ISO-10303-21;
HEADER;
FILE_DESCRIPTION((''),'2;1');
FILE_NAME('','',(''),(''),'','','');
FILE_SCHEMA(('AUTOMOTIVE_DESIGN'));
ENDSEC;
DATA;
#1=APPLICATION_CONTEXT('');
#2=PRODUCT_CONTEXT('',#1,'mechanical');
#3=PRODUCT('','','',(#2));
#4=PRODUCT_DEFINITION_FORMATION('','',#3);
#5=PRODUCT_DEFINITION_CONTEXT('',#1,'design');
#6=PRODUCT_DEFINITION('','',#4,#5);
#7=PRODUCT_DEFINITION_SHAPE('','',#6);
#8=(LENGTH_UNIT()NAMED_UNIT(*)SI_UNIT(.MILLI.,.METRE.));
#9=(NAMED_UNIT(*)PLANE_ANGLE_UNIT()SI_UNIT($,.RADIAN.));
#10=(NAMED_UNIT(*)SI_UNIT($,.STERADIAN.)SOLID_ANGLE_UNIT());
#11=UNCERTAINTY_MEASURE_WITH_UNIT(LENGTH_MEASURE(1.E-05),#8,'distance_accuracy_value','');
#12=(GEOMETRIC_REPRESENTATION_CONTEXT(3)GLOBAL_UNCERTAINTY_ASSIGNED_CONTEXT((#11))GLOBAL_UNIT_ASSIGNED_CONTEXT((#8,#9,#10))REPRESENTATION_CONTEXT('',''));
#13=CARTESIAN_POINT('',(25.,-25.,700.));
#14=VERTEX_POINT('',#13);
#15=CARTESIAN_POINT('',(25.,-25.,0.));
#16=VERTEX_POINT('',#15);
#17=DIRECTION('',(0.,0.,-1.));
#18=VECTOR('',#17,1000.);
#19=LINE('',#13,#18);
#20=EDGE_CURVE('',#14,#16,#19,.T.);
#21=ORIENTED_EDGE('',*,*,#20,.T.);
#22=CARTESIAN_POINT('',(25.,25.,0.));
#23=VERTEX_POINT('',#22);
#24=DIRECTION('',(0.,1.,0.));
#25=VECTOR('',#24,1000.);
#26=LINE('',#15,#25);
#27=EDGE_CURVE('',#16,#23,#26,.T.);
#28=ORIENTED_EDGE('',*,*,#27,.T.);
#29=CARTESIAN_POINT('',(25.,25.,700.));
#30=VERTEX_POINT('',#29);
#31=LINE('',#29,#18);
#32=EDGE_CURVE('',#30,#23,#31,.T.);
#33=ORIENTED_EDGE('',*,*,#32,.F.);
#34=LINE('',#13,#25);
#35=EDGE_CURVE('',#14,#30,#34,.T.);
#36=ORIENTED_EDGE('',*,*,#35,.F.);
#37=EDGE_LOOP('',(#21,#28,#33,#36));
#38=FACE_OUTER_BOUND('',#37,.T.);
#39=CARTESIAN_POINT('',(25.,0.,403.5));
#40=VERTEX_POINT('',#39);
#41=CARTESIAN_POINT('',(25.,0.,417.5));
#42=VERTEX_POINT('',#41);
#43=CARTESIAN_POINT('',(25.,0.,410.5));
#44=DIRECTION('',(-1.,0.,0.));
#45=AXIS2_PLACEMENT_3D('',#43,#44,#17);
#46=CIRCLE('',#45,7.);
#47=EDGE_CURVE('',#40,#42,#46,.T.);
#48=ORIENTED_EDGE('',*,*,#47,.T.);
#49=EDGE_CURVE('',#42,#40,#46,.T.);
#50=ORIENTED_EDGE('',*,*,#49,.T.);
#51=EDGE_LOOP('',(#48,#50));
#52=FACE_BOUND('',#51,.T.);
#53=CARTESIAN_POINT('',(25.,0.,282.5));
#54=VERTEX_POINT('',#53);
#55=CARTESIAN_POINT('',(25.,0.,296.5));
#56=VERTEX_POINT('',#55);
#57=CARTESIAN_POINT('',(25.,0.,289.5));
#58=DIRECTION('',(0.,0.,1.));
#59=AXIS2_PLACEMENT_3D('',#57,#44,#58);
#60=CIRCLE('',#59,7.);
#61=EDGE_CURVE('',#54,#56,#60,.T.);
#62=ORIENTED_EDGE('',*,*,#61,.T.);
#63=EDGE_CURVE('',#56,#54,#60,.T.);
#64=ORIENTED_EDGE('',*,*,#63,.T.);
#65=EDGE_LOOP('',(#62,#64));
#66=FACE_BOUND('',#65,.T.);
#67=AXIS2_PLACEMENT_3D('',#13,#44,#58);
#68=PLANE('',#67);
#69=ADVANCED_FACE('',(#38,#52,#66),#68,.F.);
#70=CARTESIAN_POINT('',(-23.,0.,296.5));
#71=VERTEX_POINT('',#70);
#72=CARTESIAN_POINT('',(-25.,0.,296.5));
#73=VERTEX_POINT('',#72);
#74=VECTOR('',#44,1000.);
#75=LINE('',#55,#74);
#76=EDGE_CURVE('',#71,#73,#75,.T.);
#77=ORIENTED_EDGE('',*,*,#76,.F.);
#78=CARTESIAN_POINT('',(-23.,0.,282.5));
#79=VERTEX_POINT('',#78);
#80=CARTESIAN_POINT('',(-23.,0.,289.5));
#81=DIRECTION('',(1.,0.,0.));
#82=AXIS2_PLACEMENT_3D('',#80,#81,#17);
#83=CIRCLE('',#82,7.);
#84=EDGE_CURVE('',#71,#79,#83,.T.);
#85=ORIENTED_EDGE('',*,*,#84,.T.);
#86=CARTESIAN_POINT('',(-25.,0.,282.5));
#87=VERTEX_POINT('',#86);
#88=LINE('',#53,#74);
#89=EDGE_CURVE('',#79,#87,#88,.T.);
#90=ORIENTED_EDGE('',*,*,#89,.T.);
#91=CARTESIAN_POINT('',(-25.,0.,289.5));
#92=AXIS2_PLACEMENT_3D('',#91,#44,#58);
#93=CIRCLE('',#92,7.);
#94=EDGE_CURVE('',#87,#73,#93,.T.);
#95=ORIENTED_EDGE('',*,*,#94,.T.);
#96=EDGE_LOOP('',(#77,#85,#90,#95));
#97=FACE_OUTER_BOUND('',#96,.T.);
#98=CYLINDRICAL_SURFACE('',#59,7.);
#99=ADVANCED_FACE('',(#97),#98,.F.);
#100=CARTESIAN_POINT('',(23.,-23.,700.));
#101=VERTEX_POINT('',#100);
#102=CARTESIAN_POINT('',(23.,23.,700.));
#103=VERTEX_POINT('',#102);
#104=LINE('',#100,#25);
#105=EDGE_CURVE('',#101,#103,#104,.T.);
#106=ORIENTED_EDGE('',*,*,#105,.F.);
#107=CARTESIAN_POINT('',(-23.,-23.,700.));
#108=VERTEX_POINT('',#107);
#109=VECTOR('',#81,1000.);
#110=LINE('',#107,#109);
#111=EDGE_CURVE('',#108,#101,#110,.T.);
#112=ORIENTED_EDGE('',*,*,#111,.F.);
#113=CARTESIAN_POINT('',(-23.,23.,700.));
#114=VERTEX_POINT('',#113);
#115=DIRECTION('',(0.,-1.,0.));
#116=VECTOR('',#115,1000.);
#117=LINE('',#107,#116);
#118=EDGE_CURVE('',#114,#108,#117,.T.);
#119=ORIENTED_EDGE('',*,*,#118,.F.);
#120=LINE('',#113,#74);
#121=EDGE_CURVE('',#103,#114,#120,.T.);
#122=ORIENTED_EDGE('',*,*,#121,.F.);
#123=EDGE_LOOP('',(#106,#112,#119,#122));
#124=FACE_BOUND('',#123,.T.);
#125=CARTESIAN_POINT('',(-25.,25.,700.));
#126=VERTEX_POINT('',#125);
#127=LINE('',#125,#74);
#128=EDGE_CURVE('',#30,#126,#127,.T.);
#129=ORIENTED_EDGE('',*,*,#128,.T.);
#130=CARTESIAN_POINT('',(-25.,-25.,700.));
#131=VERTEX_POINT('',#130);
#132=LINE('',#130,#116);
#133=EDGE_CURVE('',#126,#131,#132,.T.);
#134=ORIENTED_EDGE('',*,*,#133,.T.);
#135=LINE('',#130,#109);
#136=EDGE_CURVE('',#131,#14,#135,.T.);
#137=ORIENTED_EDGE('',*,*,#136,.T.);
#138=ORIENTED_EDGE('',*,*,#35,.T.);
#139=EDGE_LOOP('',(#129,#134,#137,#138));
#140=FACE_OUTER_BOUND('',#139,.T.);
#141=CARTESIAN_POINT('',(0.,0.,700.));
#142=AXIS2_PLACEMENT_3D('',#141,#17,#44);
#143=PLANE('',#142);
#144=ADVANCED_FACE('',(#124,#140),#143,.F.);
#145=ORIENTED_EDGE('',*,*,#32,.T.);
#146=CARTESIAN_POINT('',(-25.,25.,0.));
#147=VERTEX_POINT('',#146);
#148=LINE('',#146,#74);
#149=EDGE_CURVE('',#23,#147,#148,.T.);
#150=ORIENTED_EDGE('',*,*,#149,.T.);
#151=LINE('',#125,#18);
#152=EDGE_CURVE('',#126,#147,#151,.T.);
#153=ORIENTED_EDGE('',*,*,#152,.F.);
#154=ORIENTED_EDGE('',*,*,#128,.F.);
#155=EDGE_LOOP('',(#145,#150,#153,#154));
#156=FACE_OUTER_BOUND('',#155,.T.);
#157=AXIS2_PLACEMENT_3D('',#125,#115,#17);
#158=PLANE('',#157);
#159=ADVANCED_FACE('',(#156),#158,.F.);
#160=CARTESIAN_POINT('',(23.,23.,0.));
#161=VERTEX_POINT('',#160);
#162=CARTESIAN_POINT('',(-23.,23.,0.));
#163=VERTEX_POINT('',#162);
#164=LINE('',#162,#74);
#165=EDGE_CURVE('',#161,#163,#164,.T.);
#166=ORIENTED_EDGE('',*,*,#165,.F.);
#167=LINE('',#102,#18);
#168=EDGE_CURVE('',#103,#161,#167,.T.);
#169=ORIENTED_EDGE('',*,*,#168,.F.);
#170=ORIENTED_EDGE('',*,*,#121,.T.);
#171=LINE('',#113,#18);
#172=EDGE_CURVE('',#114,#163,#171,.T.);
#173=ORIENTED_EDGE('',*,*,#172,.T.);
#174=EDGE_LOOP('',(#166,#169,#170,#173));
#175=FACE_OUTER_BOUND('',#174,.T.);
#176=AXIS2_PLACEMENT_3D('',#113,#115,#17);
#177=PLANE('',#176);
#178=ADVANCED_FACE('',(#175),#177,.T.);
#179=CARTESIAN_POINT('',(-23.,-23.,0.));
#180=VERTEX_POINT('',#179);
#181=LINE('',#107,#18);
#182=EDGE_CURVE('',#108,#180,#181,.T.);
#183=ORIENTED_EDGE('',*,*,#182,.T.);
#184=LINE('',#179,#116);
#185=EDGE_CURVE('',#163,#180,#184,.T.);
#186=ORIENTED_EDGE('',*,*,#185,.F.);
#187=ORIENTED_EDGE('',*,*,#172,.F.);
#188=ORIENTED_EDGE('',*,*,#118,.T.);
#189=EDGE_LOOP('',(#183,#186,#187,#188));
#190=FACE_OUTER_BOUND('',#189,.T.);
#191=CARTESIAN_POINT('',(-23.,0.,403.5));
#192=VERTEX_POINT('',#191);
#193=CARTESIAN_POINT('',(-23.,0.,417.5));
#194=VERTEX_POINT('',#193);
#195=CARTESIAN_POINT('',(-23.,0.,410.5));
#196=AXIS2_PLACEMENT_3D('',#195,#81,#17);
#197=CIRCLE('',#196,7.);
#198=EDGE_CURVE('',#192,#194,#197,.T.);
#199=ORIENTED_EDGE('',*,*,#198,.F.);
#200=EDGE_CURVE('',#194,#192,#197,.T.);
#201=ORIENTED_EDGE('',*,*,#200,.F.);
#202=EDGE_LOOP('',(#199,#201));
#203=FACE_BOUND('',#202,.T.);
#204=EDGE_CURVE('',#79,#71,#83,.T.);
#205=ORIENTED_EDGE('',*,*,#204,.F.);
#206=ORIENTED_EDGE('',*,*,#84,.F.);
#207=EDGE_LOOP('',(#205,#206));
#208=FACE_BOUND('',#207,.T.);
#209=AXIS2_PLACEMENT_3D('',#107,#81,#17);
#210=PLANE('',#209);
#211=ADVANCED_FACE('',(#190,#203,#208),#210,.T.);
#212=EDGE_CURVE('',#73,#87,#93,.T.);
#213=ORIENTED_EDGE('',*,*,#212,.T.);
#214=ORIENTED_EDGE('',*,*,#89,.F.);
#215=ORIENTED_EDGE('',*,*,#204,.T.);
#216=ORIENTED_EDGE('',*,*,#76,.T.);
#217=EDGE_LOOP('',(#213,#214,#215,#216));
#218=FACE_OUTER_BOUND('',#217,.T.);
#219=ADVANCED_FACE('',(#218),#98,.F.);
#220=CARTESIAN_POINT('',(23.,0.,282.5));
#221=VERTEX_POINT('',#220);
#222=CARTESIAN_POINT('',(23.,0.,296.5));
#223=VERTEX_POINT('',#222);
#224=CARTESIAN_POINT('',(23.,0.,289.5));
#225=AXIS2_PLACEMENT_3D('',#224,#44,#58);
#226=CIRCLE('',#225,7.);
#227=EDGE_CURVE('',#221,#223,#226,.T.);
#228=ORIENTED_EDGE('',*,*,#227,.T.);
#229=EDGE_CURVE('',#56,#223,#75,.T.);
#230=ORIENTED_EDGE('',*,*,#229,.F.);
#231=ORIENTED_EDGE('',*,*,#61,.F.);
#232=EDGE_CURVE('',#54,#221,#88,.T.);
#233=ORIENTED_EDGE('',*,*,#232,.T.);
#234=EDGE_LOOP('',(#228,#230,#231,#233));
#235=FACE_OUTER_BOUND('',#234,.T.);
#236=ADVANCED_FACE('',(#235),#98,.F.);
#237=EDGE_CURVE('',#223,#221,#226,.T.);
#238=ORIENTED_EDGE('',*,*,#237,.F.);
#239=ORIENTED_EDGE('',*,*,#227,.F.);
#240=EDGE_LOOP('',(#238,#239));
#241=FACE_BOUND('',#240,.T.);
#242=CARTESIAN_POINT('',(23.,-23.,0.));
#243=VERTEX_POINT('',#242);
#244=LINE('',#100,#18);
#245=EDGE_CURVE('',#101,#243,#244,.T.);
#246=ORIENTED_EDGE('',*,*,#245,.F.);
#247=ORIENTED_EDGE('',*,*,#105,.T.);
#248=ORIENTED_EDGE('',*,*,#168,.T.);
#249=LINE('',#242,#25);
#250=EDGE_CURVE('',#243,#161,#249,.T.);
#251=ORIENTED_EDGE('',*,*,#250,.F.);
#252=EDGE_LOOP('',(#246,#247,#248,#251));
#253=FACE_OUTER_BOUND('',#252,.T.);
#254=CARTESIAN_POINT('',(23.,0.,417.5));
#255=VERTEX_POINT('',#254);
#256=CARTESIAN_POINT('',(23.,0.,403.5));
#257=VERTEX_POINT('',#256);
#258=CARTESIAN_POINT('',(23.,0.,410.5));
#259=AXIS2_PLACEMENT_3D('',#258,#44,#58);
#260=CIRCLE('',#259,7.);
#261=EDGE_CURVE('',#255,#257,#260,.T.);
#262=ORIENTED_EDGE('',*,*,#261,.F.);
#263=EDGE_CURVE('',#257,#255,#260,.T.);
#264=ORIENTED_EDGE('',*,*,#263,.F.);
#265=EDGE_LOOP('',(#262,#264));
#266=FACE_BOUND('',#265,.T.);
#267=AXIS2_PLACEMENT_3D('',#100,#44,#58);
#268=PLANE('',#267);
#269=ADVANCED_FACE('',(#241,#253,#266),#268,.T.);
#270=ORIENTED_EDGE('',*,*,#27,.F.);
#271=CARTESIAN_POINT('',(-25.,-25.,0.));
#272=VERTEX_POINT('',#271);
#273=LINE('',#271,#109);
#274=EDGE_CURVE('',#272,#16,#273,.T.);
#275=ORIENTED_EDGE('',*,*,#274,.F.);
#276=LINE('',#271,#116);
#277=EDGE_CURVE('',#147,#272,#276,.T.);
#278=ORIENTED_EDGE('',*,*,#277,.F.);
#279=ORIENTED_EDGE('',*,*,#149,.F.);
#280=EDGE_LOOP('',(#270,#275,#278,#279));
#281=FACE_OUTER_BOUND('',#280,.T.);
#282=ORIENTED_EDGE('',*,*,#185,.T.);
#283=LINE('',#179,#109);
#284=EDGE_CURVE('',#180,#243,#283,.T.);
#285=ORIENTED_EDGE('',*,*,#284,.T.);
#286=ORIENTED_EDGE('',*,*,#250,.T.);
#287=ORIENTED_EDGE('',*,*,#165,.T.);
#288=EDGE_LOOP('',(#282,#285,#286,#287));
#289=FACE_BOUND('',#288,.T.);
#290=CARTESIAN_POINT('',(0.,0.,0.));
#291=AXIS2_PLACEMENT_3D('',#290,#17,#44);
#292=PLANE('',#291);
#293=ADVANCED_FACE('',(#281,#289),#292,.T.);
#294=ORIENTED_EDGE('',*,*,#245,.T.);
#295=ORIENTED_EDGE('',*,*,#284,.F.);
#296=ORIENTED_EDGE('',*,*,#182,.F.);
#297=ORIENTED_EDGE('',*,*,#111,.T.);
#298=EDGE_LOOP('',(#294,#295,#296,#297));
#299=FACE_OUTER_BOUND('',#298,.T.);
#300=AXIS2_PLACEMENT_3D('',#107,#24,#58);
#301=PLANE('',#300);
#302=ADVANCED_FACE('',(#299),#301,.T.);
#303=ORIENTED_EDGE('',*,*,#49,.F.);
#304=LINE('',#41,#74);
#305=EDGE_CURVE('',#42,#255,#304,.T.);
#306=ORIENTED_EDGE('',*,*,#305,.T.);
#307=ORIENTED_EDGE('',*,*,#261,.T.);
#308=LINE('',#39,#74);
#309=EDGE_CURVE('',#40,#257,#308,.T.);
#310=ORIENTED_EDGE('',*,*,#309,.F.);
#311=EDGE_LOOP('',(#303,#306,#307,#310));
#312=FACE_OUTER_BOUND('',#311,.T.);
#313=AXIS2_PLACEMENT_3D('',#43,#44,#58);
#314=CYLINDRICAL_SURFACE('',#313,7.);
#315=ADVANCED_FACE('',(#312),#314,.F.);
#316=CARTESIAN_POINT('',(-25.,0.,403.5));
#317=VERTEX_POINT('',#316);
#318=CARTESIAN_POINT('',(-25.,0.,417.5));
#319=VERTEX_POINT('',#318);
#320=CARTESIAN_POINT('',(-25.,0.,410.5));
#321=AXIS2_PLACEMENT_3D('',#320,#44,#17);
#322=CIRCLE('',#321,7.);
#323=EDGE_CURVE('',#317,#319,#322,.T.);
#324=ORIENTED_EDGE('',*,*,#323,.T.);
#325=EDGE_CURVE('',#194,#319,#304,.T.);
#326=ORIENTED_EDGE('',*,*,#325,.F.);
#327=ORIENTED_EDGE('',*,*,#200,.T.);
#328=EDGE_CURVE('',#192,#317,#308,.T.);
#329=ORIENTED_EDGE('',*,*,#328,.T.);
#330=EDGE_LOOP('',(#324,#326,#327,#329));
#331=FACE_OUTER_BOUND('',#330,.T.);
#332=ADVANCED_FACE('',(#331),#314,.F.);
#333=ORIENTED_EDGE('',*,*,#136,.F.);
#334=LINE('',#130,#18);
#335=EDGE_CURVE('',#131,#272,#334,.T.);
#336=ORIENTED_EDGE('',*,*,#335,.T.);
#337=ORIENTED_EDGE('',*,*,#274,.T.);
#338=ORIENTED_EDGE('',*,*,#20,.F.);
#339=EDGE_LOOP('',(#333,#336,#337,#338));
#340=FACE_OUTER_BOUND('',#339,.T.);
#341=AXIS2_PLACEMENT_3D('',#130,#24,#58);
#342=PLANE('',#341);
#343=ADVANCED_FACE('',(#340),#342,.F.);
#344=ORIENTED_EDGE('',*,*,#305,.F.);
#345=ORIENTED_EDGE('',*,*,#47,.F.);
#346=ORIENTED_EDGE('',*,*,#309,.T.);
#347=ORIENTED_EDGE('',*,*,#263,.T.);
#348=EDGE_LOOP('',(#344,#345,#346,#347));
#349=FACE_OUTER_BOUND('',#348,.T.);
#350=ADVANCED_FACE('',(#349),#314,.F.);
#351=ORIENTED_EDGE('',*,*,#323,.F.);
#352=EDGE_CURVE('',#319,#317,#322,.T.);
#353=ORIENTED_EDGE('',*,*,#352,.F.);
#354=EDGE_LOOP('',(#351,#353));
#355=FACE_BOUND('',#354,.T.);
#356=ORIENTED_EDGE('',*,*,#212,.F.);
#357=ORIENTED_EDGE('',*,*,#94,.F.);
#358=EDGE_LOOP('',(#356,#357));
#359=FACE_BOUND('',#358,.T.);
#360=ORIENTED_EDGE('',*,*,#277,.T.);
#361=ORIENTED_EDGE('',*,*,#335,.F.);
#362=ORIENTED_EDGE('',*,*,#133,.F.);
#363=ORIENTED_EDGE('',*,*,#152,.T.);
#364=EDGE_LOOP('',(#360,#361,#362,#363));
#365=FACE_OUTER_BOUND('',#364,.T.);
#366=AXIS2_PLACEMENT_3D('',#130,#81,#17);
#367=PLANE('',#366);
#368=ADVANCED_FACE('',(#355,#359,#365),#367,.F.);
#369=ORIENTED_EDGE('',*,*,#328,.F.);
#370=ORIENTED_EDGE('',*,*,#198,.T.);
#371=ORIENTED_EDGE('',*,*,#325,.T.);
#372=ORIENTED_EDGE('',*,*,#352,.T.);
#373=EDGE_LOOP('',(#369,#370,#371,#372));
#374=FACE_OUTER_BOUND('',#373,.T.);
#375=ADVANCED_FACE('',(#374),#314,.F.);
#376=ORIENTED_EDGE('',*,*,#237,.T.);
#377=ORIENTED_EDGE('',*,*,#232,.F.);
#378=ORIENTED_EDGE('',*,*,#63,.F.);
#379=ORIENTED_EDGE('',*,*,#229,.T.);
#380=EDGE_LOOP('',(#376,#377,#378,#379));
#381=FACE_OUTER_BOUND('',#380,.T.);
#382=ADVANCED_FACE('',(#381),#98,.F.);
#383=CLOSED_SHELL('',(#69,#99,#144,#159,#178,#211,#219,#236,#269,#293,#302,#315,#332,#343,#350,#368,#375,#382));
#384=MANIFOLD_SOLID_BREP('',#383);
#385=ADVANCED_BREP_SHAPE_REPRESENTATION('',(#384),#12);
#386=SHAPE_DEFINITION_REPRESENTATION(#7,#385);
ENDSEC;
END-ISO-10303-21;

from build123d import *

# Parameters (mm, degrees)
SKETCH1_W           = 50
SKETCH1_H           = 50
SKETCH1_W_2         = 46
SKETCH1_H_2         = 46
BOSS_EXTRUDE1_DEPTH = 700
SKETCH2_R           = 7
CUT_EXTRUDE1_DEPTH  = 703.228595259


with BuildPart() as part:
    # Sketch1 → Boss-Extrude1 (new body)
    with BuildSketch(Plane.XY):
        Rectangle(SKETCH1_W, SKETCH1_H)
        Rectangle(SKETCH1_W_2, SKETCH1_H_2, mode=Mode.SUBTRACT)
    extrude(amount=BOSS_EXTRUDE1_DEPTH)

    # Sketch2 → Cut-Extrude1 (cut, through all)
    with BuildSketch(Plane.ZY.offset(25)):
        with Locations((289.5, 0)):
            Circle(SKETCH2_R)
        with Locations(Location((410.5, 0, 0), (0, 0, 180))):
            Circle(SKETCH2_R)
    extrude(amount=-CUT_EXTRUDE1_DEPTH, mode=Mode.SUBTRACT)


solid = part.part
